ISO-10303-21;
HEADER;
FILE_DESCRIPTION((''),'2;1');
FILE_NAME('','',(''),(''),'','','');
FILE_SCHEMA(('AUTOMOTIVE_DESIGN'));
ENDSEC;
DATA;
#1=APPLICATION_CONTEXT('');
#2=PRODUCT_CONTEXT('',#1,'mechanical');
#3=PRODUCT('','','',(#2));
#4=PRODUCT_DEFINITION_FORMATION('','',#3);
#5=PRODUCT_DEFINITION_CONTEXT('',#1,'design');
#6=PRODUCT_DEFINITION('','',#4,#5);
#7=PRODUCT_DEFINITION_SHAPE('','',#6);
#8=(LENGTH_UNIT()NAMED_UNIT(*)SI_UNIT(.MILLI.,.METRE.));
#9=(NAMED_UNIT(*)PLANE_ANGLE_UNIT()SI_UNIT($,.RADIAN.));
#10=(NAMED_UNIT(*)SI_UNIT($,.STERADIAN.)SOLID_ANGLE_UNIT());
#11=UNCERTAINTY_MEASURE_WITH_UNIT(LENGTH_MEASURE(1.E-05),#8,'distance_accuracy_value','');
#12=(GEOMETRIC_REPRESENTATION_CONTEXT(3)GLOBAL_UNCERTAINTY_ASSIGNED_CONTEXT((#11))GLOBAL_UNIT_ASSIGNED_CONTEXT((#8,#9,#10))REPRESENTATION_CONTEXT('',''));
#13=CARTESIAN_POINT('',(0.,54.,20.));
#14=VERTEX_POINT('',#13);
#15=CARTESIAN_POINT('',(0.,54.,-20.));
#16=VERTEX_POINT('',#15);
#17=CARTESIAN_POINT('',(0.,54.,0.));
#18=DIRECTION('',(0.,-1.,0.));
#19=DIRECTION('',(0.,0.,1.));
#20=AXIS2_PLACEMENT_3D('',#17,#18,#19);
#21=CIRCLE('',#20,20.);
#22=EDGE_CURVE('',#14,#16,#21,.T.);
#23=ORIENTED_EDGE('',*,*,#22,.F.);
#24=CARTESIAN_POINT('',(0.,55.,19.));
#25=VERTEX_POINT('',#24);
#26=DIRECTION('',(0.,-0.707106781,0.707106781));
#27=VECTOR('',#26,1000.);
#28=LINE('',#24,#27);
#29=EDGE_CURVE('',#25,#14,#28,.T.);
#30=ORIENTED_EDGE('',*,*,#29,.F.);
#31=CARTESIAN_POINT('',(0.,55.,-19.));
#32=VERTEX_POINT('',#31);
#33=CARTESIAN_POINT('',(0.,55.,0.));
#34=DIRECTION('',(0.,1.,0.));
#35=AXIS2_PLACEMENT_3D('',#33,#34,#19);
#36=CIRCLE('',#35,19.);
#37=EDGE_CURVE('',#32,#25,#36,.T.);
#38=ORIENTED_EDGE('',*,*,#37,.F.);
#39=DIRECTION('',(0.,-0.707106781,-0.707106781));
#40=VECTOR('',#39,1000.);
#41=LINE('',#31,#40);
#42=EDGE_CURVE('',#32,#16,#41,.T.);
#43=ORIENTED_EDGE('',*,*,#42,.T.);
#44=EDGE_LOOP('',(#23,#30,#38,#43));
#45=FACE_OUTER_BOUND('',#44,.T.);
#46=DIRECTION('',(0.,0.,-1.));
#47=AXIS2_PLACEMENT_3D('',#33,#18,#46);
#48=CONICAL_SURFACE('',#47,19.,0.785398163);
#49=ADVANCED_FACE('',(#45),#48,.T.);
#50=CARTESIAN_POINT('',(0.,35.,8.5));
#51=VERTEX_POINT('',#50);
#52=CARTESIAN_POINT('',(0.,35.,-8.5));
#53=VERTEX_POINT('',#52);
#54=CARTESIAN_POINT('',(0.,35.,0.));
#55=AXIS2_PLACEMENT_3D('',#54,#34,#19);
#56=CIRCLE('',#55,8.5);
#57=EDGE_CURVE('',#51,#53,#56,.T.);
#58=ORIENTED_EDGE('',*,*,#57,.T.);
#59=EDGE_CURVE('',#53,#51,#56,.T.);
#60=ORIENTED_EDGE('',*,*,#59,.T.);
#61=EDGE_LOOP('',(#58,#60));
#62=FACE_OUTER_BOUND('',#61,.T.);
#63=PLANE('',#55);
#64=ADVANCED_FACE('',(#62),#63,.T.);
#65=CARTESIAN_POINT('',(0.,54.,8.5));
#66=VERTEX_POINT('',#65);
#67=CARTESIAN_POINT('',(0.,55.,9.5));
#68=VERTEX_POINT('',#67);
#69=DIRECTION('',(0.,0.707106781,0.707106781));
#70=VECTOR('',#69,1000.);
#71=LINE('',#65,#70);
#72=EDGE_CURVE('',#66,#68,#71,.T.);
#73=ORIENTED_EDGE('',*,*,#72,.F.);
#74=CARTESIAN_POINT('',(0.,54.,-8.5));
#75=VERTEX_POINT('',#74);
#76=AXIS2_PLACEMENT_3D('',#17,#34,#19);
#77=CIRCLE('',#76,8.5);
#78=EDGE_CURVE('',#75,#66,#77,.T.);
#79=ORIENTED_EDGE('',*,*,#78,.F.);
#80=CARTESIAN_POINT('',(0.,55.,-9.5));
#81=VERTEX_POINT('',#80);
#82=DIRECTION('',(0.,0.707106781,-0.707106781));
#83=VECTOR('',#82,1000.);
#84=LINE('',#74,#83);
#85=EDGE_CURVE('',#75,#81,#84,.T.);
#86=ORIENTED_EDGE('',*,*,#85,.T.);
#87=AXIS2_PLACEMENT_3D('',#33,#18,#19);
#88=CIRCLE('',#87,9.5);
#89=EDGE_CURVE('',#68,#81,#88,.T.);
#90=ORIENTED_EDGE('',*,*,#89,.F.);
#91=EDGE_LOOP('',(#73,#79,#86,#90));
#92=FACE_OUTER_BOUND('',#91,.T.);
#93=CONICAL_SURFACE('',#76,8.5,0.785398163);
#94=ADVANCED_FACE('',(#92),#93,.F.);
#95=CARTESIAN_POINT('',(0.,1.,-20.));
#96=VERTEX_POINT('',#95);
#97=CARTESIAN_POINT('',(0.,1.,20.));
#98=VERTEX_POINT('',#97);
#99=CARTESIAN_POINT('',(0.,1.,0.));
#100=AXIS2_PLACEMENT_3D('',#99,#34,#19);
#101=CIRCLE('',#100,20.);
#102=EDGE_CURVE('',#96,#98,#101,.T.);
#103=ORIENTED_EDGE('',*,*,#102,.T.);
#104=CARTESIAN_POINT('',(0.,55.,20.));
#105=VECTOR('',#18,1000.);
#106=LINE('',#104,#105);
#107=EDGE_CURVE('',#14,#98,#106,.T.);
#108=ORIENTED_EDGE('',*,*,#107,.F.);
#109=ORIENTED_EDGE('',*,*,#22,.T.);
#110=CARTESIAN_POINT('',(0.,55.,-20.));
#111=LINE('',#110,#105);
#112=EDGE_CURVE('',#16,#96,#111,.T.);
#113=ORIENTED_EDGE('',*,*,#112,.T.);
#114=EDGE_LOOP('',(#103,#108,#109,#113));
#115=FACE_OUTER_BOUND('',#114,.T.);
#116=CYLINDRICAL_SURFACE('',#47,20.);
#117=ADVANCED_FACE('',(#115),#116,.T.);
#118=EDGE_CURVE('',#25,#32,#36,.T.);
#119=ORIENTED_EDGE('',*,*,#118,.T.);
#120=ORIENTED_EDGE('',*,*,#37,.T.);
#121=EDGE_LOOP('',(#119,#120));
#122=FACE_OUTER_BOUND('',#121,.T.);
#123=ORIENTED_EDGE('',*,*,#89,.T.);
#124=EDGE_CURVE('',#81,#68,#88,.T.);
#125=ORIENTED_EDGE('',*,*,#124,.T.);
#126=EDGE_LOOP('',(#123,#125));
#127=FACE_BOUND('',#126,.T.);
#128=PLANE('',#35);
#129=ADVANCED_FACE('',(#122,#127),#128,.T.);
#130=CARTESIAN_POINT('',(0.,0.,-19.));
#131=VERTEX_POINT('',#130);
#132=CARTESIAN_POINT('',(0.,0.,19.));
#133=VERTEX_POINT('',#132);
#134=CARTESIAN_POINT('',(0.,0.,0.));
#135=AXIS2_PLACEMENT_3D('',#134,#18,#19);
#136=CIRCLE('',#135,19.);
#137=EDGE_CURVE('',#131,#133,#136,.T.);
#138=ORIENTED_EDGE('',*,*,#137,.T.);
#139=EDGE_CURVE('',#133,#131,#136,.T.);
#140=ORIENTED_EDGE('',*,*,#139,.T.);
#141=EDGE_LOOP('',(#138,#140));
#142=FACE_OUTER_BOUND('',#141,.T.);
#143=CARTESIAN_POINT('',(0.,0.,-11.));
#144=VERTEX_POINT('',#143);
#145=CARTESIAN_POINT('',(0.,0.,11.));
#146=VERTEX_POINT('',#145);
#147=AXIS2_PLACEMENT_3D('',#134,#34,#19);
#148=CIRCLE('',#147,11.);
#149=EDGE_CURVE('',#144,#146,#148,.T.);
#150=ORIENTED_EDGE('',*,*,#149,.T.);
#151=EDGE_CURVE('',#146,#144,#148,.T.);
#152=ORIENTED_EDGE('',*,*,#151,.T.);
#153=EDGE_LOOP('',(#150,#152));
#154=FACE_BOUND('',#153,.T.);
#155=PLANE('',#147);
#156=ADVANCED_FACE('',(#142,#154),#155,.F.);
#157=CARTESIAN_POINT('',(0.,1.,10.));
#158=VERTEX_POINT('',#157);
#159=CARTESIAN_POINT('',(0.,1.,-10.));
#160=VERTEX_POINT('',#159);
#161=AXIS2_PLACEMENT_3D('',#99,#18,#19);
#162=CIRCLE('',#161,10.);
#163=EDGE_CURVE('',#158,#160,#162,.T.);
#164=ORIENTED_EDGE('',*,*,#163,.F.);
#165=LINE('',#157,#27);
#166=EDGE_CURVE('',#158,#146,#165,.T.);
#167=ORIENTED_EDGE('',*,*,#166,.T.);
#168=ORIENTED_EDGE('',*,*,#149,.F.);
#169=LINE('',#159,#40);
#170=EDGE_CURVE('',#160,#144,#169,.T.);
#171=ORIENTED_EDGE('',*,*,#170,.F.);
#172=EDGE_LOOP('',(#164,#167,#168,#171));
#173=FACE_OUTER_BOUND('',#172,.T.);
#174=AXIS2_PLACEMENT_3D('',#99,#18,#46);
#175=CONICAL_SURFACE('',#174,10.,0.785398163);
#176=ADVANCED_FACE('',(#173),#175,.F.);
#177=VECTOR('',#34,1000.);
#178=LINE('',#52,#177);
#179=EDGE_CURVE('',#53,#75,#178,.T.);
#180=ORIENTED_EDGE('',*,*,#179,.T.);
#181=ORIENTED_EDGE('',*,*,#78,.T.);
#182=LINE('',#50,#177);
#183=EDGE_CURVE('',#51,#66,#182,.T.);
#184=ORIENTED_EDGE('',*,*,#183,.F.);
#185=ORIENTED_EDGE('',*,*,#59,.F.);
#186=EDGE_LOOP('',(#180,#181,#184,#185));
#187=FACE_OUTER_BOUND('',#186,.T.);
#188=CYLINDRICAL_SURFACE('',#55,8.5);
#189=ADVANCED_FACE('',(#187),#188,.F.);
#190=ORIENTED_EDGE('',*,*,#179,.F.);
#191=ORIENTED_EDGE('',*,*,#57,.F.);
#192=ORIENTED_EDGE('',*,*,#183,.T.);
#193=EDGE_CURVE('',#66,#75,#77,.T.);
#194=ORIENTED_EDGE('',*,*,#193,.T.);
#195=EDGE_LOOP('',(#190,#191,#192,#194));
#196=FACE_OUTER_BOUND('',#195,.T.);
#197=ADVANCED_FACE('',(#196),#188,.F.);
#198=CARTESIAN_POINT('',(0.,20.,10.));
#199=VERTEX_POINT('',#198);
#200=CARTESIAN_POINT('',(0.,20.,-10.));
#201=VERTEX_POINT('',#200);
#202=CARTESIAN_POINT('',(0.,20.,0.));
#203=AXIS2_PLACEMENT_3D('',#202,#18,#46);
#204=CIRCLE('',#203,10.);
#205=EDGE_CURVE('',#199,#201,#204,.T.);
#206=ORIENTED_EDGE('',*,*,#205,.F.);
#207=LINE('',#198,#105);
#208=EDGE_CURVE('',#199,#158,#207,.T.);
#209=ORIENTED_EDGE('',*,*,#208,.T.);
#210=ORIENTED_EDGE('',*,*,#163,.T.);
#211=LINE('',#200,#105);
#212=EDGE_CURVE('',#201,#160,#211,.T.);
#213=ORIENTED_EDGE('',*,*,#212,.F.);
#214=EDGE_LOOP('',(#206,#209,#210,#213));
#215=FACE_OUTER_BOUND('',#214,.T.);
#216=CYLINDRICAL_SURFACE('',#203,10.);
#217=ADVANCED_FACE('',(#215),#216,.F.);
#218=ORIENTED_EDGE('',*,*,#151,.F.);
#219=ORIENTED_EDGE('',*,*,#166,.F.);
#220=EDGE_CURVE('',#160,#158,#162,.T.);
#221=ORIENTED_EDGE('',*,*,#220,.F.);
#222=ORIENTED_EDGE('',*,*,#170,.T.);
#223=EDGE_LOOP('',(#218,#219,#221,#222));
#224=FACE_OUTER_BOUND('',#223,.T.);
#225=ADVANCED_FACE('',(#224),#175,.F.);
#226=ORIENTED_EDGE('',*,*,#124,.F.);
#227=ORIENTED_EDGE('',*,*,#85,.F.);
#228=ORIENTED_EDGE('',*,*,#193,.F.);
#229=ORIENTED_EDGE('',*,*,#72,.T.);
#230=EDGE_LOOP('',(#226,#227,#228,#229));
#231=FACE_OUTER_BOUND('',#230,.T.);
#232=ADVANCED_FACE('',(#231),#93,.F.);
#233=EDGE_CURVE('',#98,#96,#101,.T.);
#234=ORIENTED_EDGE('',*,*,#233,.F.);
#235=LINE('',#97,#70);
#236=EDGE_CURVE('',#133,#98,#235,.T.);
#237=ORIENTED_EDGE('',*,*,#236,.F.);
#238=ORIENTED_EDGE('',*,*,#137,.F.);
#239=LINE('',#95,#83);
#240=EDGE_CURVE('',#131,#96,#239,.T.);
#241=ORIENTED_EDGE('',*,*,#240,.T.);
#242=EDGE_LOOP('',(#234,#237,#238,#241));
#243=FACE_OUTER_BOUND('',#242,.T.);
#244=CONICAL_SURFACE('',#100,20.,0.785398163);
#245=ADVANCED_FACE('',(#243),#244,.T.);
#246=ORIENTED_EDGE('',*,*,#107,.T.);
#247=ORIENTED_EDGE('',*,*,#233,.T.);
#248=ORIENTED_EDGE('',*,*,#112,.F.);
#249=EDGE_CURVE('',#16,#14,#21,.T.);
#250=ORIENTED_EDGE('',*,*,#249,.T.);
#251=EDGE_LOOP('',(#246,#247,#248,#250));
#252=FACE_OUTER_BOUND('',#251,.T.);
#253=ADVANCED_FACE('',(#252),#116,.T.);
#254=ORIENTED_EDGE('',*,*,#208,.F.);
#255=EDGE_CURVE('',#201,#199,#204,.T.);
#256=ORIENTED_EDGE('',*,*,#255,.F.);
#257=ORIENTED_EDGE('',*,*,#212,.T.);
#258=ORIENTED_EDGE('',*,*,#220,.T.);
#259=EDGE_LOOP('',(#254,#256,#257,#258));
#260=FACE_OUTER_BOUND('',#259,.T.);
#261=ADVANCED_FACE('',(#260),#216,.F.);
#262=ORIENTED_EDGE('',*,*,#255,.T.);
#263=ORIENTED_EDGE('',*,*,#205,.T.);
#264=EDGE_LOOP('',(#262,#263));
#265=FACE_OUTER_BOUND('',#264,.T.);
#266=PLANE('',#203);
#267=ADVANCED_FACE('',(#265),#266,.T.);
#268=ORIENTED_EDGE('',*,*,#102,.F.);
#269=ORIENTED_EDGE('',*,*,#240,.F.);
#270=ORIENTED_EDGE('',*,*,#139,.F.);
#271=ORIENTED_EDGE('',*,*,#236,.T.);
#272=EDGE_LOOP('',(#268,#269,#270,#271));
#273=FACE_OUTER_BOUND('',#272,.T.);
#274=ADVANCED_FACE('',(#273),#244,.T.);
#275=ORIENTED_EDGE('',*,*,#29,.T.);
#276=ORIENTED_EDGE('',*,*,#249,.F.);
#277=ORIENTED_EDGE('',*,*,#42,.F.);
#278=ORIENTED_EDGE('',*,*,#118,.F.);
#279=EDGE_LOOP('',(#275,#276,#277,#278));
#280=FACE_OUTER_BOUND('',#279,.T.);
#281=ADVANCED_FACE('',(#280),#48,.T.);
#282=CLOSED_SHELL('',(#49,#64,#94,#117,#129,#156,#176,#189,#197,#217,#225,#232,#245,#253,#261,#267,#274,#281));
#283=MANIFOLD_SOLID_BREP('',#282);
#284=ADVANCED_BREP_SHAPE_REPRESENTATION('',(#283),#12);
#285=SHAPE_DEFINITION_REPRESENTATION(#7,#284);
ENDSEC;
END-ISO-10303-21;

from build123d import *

# Parameters (mm, degrees)
SKETCH_1_R          = 20
EXTRUDE_1_DEPTH     = 55
SKETCH_2_R          = 8.5
CUT_EXTRUDE_1_DEPTH = 20
SKETCH_3_R          = 10
CUT_EXTRUDE_2_DEPTH = 20
CHAMFER_1_SIZE      = 1


with BuildPart() as part:
    # 草图1 → 凸台-拉伸1 (new body)
    with BuildSketch(Plane(origin=(0, 0, 0), x_dir=(1, 0, 0), z_dir=(0, 1, 0))):
        with Locations(Location((0, 0, 0), (0, 0, 270))):
            Circle(SKETCH_1_R)
    extrude(amount=EXTRUDE_1_DEPTH)

    # 草图2 → 切除-拉伸1 (cut)
    with BuildSketch(Plane(origin=(0, 55, 0), x_dir=(1, 0, 0), z_dir=(0, 1, 0))):
        with Locations(Location((0, 0, 0), (0, 0, 270))):
            Circle(SKETCH_2_R)
    extrude(amount=-CUT_EXTRUDE_1_DEPTH, mode=Mode.SUBTRACT)

    # 草图3 → 切除-拉伸2 (cut)
    with BuildSketch(Plane.XZ):
        with Locations(Location((0, 0, 0), (0, 0, 270))):
            Circle(SKETCH_3_R)
    extrude(amount=-CUT_EXTRUDE_2_DEPTH, mode=Mode.SUBTRACT)

    # 倒角1
    chamfer_1_edges = [part.edges().sort_by_distance(p)[0] for p in [
        (0, 0, 10),
        (0, 0, -20),
        (0, 55, -20),
        (0, 55, -8.5),
    ]]
    chamfer(chamfer_1_edges, length=CHAMFER_1_SIZE)


solid = part.part
